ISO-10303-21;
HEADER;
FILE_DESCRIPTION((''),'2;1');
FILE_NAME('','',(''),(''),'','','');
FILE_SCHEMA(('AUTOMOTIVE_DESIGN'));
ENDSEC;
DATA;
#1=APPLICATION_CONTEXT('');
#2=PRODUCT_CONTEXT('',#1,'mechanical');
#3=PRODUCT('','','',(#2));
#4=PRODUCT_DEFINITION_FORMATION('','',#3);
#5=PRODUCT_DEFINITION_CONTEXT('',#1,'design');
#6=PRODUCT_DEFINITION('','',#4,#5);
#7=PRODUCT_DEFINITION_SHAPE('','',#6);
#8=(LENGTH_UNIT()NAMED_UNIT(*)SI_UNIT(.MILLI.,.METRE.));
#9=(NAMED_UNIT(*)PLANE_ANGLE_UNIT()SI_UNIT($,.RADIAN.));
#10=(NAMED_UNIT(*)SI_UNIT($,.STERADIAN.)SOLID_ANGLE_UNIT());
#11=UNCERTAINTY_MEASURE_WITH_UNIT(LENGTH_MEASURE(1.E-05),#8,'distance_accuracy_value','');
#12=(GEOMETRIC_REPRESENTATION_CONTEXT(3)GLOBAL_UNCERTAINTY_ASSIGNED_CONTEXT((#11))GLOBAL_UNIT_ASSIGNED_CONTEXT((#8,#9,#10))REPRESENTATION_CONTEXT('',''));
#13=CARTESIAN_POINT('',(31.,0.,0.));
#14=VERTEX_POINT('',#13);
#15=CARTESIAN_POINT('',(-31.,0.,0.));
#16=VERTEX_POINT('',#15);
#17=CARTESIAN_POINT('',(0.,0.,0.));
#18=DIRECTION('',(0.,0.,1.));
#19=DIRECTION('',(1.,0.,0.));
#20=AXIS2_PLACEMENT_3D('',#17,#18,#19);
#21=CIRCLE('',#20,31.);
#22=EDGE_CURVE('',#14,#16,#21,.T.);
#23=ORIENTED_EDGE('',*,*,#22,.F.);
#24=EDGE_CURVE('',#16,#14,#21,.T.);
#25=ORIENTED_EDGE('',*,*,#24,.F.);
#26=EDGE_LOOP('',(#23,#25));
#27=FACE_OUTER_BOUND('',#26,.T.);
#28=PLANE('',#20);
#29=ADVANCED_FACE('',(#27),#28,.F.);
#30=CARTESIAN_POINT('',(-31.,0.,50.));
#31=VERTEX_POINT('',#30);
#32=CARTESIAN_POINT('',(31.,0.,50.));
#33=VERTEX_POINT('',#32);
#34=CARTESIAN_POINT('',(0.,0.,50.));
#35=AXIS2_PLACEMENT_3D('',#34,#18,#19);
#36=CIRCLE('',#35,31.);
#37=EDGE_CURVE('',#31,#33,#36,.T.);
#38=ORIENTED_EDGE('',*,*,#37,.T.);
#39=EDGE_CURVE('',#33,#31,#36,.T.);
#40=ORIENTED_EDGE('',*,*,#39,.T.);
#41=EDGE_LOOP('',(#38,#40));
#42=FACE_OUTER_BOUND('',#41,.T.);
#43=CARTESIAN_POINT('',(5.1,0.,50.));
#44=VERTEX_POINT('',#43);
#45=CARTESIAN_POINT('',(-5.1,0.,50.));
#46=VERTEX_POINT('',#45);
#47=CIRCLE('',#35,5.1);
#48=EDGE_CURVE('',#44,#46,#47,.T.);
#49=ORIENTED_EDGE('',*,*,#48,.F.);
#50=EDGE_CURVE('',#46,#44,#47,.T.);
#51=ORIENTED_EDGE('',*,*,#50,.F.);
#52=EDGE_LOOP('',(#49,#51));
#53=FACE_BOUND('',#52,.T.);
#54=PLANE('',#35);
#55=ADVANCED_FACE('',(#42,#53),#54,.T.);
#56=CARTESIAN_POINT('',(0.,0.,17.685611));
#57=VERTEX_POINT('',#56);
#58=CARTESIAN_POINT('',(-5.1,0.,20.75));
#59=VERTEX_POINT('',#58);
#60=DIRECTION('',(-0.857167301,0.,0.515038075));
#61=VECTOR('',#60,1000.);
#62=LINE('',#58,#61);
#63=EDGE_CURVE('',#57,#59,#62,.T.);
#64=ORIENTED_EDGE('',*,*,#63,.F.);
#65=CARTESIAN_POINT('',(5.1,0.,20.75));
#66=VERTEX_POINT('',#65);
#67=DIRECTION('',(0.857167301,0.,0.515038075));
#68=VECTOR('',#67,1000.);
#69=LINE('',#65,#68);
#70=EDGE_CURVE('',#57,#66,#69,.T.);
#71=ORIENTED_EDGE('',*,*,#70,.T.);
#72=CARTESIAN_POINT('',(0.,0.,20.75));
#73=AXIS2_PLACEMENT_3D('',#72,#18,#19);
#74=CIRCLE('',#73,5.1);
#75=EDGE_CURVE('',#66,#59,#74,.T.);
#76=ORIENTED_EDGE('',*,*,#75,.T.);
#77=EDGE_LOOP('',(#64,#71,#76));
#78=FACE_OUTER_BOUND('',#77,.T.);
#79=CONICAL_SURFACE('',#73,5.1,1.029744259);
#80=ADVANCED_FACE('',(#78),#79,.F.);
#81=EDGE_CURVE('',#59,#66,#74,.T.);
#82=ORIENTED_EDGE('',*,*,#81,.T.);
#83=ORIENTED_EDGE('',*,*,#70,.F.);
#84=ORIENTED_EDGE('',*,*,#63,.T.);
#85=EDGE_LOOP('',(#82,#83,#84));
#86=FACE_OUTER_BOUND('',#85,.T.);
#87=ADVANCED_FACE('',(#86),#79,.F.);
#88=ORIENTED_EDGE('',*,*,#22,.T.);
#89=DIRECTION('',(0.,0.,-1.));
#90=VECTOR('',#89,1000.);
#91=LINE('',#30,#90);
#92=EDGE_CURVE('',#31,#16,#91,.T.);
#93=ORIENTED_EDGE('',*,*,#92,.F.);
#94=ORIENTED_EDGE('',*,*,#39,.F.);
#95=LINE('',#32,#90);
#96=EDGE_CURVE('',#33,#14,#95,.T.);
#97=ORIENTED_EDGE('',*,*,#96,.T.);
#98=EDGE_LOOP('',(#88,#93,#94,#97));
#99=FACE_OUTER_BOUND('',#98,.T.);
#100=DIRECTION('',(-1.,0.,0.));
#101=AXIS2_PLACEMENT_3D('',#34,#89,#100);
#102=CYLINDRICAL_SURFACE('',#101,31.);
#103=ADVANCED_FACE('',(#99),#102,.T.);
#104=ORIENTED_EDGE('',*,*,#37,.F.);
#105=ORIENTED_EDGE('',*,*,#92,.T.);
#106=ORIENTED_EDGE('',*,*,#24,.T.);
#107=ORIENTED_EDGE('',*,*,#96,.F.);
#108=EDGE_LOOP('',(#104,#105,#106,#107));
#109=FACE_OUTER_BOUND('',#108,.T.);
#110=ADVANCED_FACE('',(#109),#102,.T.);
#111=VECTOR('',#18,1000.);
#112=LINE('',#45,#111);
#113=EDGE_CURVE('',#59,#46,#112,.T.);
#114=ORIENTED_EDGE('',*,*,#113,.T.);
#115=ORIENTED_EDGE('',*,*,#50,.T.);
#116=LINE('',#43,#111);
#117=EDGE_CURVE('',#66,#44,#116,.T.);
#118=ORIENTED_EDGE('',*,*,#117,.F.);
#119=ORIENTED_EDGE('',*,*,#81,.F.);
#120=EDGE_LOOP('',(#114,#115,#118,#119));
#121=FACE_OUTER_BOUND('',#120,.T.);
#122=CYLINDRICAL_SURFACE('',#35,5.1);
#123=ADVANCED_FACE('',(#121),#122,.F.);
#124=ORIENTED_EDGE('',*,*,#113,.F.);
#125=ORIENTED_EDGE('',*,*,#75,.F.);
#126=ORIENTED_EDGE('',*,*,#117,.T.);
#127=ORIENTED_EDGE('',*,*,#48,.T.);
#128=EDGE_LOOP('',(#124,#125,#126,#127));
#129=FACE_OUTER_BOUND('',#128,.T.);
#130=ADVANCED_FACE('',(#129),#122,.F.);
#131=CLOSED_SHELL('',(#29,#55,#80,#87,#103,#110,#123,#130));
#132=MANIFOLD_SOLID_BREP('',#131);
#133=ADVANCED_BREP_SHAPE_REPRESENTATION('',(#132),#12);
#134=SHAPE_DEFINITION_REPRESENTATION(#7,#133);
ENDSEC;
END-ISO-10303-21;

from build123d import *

# Parameters (mm, degrees)
SKETCH1_R              = 31
BOSS_EXTRUDE1_DEPTH    = 50
M12_TAPPED_HOLE1_D     = 10.2
M12_TAPPED_HOLE1_DEPTH = 29.25
M12_TAPPED_HOLE1_TIP   = 3.064389157


with BuildPart() as part:
    # Sketch1 → Boss-Extrude1 (new body)
    with BuildSketch(Plane.XY):
        Circle(SKETCH1_R)
    extrude(amount=BOSS_EXTRUDE1_DEPTH)

    # M12 Tapped Hole1
    with Locations(Plane.XY.offset(50)):
        with Locations((0, 0)):
            Hole(M12_TAPPED_HOLE1_D / 2, depth=M12_TAPPED_HOLE1_DEPTH)
            with Locations((0, 0, -(M12_TAPPED_HOLE1_DEPTH + M12_TAPPED_HOLE1_TIP / 2))):  # 118° drill point
                Cone(0, M12_TAPPED_HOLE1_D / 2, M12_TAPPED_HOLE1_TIP, mode=Mode.SUBTRACT)


solid = part.part
